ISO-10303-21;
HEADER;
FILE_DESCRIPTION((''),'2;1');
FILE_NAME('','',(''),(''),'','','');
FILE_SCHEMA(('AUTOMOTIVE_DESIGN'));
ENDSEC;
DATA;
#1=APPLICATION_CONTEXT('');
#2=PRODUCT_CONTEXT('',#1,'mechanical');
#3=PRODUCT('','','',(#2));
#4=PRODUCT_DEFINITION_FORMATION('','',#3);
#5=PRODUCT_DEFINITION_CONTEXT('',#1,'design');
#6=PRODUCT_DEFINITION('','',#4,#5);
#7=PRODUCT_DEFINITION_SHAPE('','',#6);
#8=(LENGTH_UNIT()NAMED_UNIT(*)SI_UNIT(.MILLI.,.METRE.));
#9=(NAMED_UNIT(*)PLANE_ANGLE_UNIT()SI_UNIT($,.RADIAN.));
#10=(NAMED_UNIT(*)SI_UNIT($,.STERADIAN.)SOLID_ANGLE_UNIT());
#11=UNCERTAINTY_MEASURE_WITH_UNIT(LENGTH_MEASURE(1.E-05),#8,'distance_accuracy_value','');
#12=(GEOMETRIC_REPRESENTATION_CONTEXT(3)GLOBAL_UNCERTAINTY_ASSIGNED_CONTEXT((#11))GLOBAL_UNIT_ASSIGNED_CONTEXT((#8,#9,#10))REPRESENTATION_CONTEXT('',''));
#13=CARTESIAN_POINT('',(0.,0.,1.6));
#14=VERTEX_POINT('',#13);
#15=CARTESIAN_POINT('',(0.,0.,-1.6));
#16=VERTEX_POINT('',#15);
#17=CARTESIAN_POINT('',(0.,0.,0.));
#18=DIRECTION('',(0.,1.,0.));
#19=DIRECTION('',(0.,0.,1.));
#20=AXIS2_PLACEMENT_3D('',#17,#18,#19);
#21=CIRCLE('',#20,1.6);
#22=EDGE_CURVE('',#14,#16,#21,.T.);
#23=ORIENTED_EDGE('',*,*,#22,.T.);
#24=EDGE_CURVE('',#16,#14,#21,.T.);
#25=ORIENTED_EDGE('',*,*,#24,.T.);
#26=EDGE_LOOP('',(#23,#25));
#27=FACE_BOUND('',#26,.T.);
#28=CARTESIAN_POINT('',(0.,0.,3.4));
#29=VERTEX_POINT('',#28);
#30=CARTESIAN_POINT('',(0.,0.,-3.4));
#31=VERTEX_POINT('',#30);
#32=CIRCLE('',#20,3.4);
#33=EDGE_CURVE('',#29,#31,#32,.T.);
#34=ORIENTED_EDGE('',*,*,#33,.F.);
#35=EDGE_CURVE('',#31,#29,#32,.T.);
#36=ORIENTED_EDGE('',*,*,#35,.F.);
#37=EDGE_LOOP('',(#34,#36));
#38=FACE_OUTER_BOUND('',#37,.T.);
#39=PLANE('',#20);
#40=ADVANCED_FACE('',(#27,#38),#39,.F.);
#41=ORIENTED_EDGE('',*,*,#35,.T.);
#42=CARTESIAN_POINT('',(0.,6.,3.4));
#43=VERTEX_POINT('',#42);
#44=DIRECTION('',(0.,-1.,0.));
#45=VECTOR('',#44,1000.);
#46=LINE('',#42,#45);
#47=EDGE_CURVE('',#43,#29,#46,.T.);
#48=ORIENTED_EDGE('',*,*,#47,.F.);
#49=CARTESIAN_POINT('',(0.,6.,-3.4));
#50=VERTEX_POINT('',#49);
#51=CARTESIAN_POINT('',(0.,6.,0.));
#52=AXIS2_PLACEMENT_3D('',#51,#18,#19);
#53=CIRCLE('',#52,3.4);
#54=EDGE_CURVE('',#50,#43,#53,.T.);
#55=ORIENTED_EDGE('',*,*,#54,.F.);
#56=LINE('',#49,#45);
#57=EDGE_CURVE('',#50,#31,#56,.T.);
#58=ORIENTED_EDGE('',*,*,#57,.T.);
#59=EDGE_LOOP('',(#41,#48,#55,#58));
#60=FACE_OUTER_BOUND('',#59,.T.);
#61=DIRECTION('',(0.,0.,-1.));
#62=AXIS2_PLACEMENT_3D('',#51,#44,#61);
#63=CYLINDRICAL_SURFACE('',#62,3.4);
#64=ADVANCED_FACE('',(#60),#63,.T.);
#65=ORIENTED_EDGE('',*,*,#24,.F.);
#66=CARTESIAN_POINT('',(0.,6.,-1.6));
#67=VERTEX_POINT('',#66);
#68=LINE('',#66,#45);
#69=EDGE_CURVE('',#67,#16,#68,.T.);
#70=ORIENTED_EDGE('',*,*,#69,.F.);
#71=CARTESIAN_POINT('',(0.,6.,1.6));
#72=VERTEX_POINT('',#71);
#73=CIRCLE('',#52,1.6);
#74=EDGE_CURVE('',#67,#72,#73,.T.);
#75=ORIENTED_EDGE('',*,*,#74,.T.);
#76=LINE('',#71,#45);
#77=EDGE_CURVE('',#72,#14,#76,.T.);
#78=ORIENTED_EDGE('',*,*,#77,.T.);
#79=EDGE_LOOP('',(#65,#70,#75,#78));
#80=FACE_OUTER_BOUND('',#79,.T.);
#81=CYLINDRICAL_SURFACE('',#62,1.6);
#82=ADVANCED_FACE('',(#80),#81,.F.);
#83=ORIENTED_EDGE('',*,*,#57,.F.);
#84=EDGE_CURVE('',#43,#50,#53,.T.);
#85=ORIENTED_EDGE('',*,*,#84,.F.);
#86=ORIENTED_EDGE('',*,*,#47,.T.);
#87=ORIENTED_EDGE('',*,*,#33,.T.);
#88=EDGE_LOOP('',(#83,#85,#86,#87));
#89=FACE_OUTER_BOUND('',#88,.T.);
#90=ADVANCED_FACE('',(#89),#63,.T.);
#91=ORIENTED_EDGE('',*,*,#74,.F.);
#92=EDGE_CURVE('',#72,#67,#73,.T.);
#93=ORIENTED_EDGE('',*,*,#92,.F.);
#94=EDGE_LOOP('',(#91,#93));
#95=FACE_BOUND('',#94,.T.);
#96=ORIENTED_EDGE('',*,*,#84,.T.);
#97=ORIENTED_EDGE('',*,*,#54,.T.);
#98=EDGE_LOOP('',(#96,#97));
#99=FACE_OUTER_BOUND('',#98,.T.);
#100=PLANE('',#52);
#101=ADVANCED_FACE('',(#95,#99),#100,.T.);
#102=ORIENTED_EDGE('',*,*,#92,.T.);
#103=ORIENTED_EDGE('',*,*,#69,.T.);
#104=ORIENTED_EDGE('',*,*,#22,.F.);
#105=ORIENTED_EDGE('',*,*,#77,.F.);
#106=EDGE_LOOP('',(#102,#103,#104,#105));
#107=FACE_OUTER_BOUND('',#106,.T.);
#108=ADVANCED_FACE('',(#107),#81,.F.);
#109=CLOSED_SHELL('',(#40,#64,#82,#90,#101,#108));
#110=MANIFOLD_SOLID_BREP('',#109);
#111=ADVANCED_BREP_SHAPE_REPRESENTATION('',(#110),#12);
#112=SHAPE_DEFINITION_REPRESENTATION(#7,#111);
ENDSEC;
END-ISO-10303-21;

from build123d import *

# Parameters (mm, degrees)
SKETCH_1_R      = 3.4
SKETCH_1_R_2    = 1.6
EXTRUDE_1_DEPTH = 6


with BuildPart() as part:
    # 草图1 → 凸台-拉伸1 (new body)
    with BuildSketch(Plane(origin=(0, 0, 0), x_dir=(1, 0, 0), z_dir=(0, 1, 0))):
        with Locations(Location((0, 0, 0), (0, 0, 270))):
            Circle(SKETCH_1_R)
        with Locations(Location((0, 0, 0), (0, 0, 270))):
            Circle(SKETCH_1_R_2, mode=Mode.SUBTRACT)
    extrude(amount=EXTRUDE_1_DEPTH)


solid = part.part
